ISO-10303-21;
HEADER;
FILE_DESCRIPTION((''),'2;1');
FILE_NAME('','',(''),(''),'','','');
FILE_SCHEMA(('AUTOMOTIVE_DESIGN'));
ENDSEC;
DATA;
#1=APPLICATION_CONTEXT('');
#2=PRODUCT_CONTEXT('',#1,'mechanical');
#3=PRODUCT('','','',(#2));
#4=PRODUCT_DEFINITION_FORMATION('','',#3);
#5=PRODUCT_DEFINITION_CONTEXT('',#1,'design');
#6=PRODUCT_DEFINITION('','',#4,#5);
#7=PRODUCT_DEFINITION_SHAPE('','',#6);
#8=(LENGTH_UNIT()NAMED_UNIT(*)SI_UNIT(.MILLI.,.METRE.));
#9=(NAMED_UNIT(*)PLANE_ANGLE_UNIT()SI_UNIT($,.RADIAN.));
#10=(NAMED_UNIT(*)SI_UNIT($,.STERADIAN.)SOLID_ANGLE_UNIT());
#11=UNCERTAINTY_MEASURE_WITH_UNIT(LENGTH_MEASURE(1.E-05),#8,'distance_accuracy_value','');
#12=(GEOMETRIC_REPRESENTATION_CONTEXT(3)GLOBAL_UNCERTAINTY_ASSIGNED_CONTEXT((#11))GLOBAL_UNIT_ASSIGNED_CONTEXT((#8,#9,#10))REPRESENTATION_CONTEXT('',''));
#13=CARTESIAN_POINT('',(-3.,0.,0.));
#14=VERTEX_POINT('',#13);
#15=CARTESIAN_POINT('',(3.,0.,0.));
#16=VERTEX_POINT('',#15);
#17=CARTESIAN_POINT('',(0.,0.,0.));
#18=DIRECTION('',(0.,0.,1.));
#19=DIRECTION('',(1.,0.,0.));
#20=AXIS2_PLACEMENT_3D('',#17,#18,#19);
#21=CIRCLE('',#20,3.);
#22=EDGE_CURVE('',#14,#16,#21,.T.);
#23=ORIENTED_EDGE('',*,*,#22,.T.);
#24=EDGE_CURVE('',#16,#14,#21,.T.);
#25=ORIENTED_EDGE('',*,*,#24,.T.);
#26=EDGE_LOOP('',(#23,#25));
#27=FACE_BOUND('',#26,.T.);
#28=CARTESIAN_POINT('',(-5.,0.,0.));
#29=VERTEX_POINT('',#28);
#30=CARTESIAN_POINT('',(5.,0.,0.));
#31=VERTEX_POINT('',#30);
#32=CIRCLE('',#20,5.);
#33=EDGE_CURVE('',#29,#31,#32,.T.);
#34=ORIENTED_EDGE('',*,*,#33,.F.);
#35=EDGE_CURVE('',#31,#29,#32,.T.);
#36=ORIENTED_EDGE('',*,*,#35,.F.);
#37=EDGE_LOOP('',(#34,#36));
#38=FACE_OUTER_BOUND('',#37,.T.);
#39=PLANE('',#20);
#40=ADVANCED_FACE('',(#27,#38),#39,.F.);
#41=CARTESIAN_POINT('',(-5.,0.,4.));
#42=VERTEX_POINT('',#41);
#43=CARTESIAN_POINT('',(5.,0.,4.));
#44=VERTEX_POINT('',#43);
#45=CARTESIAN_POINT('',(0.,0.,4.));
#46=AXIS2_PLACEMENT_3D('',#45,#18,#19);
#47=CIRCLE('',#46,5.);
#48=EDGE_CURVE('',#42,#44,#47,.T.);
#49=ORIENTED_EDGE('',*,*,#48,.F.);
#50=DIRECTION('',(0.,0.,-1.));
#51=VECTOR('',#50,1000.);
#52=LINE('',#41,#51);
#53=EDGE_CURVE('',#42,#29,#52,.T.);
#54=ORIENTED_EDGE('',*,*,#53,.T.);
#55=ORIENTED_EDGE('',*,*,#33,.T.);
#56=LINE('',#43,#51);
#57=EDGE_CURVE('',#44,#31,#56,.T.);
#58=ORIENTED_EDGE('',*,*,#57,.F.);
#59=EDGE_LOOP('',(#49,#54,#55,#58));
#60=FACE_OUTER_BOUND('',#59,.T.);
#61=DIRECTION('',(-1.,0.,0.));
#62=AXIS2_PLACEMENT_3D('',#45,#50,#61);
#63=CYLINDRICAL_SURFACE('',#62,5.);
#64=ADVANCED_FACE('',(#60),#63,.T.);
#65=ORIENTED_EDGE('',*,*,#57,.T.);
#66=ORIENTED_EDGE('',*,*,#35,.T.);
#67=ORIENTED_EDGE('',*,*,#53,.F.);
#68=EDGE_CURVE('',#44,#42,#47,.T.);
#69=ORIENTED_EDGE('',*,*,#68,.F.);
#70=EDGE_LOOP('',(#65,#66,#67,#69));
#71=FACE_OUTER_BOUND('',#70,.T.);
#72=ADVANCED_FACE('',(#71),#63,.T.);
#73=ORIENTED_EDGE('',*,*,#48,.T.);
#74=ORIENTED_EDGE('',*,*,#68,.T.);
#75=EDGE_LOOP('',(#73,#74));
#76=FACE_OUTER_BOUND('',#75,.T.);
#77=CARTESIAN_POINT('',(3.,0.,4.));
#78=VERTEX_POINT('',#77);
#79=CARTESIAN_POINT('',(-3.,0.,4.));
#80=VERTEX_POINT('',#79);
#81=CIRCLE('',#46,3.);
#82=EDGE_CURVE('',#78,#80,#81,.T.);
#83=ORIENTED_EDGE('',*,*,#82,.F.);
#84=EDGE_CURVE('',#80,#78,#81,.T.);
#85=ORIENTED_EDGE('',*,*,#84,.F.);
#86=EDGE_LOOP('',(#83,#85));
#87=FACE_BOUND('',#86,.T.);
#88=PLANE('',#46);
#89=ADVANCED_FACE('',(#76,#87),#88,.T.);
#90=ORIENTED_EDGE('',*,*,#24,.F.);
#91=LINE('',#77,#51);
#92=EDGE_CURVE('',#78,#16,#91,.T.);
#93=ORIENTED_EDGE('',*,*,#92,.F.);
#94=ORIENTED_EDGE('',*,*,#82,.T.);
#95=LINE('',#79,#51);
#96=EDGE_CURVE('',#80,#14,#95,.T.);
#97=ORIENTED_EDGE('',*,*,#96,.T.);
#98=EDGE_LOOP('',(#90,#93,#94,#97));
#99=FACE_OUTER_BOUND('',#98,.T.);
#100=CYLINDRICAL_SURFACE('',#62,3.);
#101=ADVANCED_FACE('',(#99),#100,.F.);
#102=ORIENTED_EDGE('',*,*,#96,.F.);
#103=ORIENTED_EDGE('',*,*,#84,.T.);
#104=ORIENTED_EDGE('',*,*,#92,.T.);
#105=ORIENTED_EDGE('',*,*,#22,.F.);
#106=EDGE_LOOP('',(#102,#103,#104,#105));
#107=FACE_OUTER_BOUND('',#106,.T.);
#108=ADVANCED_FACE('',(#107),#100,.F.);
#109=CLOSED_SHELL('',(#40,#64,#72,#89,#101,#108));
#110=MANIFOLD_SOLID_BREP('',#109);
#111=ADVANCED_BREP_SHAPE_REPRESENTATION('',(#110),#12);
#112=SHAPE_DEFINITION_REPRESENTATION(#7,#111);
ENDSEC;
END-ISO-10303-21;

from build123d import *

# Parameters (mm, degrees)
SKETCH1_R           = 5
SKETCH1_R_2         = 3
BOSS_EXTRUDE1_DEPTH = 4


with BuildPart() as part:
    # Sketch1 → Boss-Extrude1 (new body)
    with BuildSketch(Plane.XY):
        Circle(SKETCH1_R)
        Circle(SKETCH1_R_2, mode=Mode.SUBTRACT)
    extrude(amount=BOSS_EXTRUDE1_DEPTH)


solid = part.part
